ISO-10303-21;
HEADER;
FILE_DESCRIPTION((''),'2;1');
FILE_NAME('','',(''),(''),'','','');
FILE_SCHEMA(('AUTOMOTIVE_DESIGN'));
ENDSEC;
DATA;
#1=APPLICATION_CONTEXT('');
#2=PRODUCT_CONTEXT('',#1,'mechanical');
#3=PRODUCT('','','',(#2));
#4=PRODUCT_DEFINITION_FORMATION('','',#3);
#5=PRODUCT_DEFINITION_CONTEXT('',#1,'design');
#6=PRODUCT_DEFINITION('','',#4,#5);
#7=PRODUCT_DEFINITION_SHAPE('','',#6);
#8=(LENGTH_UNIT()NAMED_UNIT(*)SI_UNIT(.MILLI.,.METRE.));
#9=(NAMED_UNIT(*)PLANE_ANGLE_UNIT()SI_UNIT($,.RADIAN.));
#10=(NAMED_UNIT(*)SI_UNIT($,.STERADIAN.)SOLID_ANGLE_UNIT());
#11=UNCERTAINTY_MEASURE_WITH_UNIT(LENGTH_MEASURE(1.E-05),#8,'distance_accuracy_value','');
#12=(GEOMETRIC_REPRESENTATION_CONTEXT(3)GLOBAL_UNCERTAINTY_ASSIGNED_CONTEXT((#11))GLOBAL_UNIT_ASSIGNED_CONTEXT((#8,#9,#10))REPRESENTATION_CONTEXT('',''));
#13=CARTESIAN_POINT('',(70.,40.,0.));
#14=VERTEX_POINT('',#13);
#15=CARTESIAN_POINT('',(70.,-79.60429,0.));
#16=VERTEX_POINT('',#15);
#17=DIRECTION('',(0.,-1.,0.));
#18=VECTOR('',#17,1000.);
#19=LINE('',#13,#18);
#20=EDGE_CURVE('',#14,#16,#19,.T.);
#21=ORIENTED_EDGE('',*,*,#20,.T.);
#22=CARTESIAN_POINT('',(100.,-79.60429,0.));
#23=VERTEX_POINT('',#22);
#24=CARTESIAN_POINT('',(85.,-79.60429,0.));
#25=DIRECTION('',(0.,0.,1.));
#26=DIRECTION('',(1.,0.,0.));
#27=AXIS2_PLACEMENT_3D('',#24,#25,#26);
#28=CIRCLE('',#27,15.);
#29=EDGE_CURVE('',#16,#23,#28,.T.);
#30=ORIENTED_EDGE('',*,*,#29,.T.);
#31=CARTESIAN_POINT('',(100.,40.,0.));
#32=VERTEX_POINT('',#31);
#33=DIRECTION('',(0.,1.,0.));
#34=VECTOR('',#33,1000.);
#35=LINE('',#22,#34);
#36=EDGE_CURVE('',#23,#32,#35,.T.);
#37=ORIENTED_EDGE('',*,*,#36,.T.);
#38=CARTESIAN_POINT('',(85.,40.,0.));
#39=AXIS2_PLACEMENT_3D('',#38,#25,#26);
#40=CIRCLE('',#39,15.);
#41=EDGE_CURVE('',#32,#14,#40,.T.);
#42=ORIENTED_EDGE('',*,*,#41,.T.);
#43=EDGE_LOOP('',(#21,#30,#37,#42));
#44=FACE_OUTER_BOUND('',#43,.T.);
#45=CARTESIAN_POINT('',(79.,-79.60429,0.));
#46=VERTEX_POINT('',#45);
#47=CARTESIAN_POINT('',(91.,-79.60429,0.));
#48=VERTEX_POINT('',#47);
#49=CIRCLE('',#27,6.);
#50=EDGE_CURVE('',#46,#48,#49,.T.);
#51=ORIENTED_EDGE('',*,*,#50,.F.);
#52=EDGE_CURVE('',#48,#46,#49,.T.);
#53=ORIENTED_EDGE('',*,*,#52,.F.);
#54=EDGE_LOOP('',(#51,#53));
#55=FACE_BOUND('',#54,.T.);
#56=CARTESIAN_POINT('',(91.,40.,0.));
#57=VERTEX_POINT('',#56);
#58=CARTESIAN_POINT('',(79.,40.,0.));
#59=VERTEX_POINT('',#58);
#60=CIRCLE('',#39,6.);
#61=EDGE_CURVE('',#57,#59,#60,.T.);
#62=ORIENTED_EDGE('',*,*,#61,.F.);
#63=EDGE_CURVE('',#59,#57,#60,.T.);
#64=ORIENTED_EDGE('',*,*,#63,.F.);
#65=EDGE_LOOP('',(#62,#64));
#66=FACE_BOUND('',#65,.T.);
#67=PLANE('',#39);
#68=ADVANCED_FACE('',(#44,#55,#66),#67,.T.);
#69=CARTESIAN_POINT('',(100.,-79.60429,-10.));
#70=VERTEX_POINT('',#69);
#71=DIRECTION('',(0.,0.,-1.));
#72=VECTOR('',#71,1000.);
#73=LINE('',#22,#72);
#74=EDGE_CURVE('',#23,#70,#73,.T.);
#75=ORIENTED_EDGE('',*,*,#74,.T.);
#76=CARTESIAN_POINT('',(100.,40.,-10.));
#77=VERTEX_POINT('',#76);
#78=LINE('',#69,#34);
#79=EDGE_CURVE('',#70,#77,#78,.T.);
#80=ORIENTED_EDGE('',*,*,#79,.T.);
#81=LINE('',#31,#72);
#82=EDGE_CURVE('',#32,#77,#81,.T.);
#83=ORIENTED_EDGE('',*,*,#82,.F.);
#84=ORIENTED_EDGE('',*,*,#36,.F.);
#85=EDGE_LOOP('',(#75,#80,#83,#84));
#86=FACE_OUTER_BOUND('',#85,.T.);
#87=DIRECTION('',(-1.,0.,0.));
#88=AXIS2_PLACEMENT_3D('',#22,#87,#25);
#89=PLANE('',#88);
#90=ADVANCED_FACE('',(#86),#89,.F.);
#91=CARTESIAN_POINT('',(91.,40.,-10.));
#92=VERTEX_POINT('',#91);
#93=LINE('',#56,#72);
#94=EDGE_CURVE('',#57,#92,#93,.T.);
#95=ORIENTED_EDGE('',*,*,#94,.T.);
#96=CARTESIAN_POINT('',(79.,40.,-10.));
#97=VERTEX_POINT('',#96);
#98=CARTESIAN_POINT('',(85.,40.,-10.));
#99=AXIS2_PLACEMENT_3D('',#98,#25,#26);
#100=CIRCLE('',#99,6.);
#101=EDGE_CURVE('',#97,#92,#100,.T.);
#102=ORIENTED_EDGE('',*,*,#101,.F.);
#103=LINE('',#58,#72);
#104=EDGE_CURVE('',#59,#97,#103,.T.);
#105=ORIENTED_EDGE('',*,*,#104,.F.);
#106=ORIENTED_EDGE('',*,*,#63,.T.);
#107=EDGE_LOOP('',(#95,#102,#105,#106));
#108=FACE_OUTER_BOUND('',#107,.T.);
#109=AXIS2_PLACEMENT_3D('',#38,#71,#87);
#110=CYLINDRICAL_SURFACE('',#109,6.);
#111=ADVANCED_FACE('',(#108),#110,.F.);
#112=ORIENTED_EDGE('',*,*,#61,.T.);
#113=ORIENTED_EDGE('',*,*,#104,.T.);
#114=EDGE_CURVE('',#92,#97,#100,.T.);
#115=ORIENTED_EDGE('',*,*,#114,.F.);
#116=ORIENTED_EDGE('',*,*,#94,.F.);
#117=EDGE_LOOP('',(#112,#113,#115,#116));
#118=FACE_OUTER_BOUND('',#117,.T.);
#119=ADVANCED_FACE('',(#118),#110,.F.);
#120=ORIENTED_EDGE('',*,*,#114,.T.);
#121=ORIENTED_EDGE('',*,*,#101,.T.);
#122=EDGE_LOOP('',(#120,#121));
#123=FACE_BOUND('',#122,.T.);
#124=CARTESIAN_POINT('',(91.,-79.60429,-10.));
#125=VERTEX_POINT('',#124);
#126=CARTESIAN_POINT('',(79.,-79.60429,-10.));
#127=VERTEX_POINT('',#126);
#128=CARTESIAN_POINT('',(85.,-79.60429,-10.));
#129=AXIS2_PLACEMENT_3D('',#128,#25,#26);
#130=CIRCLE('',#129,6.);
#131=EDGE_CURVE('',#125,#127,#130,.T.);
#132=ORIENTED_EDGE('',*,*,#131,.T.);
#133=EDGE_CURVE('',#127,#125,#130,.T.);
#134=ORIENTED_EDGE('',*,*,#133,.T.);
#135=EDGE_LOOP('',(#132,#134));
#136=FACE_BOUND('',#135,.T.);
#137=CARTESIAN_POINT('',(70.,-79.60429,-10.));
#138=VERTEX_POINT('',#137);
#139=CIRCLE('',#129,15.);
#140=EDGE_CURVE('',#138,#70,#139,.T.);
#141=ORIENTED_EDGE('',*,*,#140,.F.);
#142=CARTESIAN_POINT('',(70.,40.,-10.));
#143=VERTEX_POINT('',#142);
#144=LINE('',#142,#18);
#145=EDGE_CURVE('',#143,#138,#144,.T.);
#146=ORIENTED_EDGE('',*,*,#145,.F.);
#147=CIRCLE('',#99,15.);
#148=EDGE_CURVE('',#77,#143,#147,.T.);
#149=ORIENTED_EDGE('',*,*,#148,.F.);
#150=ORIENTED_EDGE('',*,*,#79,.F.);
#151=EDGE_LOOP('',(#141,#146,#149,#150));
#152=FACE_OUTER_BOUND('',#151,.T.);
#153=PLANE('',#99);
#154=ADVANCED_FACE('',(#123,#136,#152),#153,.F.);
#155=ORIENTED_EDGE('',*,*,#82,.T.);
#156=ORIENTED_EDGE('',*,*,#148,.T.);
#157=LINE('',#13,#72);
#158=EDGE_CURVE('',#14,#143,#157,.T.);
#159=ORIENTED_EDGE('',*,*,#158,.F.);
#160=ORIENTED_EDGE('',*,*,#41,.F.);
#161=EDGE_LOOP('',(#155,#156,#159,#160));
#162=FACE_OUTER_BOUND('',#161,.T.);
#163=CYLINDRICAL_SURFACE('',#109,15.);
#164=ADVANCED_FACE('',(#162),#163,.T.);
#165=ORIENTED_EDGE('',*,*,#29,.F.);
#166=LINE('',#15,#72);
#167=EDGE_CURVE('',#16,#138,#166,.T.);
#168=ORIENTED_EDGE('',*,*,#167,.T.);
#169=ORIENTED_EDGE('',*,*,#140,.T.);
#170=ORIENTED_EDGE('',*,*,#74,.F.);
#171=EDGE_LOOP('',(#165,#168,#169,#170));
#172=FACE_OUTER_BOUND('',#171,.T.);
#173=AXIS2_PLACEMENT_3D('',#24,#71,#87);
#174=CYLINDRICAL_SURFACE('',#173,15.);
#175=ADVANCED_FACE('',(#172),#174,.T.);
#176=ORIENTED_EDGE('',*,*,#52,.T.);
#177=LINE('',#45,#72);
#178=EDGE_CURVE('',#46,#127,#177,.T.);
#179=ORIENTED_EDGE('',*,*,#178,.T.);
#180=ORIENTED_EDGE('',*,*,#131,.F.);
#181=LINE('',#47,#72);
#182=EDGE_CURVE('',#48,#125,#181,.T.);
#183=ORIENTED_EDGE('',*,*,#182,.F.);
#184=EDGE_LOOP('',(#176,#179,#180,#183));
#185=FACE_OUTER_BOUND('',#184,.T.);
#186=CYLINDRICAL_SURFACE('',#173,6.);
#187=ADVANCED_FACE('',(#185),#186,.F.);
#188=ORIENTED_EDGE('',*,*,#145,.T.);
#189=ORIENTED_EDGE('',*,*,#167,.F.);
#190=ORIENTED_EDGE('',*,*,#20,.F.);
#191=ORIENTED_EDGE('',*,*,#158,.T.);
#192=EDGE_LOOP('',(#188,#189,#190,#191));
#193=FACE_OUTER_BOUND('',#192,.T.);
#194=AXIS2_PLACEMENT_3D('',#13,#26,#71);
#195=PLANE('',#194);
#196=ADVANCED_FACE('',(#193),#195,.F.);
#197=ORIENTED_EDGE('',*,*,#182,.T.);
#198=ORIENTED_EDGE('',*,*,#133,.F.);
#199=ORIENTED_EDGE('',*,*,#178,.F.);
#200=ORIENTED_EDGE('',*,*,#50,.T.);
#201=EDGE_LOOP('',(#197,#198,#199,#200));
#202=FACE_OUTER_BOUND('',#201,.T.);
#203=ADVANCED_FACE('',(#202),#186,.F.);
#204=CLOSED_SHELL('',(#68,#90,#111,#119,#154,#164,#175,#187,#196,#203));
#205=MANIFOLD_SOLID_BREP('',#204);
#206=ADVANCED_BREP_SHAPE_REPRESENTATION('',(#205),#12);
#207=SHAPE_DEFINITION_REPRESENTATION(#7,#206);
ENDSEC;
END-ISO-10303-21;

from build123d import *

# Parameters (mm, degrees)
SKETCH2_R           = 6
BOSS_EXTRUDE1_DEPTH = 10


with BuildPart() as part:
    # Sketch2 → Boss-Extrude1 (new body)
    with BuildSketch(Plane.XY.offset(-10)):
        with BuildLine():
            Line((70, 40), (70, -79.604289692))
            ThreePointArc((70, -79.604289692), (85, -94.604289692), (100, -79.604289692))
            Line((100, -79.604289692), (100, 40))
            ThreePointArc((100, 40), (85, 55), (70, 40))
        make_face()
        with Locations((85, 40)):
            Circle(SKETCH2_R, mode=Mode.SUBTRACT)
        with Locations((85, -79.604289692)):
            Circle(SKETCH2_R, mode=Mode.SUBTRACT)
    extrude(amount=BOSS_EXTRUDE1_DEPTH)


solid = part.part
